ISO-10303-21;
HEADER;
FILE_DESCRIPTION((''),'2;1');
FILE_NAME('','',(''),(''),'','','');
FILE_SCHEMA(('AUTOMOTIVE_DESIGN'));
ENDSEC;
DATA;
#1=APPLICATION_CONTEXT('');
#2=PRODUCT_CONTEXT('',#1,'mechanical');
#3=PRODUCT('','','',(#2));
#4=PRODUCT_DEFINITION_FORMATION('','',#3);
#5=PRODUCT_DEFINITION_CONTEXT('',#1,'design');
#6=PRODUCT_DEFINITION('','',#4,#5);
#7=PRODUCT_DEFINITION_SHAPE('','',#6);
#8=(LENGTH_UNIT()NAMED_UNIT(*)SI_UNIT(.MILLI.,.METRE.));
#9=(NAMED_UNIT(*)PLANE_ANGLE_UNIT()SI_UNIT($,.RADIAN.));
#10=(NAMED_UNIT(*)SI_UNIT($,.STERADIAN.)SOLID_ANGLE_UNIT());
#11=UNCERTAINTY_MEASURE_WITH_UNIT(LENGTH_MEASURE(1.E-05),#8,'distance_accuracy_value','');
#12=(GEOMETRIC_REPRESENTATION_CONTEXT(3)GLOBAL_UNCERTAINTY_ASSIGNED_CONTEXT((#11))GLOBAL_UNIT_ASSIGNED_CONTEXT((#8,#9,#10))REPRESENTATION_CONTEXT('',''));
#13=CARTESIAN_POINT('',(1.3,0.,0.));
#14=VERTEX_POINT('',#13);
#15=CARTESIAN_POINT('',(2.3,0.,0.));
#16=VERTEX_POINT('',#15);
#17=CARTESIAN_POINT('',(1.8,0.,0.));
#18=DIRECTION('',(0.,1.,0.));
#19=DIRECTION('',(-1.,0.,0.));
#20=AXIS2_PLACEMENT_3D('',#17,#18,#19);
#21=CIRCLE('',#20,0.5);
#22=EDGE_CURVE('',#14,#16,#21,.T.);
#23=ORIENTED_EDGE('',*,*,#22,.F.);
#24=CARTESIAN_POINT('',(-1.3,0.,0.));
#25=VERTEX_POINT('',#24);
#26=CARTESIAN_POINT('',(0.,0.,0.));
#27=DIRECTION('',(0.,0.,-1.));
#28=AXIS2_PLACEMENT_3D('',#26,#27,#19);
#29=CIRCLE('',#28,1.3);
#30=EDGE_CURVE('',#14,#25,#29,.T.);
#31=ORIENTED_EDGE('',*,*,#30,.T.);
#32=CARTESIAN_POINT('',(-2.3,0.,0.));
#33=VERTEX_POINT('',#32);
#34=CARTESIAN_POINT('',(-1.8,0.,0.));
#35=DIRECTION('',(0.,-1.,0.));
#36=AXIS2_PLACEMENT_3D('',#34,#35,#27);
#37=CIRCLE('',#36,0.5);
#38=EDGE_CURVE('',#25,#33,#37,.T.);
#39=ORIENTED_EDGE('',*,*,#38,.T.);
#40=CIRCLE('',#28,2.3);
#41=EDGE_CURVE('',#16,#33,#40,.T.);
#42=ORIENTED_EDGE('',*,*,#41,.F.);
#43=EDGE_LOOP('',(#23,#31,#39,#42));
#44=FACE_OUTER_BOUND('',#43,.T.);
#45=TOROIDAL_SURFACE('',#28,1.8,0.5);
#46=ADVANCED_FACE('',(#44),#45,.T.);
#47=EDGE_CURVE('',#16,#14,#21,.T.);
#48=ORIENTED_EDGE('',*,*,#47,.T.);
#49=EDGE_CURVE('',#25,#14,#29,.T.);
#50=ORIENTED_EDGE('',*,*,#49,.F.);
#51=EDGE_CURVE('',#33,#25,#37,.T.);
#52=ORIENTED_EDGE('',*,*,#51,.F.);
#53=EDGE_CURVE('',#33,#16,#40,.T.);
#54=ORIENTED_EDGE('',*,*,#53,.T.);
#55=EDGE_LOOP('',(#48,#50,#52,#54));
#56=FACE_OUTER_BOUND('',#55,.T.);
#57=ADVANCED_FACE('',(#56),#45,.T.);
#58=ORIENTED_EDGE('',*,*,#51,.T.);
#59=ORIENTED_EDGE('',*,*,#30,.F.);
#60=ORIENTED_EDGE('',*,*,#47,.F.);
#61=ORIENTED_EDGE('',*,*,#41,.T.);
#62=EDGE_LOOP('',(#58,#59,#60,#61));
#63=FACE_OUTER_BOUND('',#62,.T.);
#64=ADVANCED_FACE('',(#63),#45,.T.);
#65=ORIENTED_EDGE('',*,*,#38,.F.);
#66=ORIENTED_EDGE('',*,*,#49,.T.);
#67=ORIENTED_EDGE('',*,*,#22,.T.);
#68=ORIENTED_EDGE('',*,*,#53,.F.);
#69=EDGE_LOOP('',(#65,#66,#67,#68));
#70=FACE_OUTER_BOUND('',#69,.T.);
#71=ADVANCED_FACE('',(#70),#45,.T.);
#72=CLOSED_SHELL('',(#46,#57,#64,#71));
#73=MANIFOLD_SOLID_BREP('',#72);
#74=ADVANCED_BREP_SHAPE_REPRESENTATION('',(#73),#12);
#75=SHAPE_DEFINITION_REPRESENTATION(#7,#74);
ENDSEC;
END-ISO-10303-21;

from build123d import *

# Parameters (mm, degrees)
SKETCH1_R = 0.5


with BuildPart() as part:
    # Sketch1 → Revolve1 (revolve)
    with BuildSketch(Plane(origin=(0, 0, 0), x_dir=(1, 0, 0), z_dir=(0, 1, 0))):
        with Locations((-1.8, 0)):
            Circle(SKETCH1_R)
    revolve(axis=Axis((0, 0, 0), (0, 0, 1)))


solid = part.part
